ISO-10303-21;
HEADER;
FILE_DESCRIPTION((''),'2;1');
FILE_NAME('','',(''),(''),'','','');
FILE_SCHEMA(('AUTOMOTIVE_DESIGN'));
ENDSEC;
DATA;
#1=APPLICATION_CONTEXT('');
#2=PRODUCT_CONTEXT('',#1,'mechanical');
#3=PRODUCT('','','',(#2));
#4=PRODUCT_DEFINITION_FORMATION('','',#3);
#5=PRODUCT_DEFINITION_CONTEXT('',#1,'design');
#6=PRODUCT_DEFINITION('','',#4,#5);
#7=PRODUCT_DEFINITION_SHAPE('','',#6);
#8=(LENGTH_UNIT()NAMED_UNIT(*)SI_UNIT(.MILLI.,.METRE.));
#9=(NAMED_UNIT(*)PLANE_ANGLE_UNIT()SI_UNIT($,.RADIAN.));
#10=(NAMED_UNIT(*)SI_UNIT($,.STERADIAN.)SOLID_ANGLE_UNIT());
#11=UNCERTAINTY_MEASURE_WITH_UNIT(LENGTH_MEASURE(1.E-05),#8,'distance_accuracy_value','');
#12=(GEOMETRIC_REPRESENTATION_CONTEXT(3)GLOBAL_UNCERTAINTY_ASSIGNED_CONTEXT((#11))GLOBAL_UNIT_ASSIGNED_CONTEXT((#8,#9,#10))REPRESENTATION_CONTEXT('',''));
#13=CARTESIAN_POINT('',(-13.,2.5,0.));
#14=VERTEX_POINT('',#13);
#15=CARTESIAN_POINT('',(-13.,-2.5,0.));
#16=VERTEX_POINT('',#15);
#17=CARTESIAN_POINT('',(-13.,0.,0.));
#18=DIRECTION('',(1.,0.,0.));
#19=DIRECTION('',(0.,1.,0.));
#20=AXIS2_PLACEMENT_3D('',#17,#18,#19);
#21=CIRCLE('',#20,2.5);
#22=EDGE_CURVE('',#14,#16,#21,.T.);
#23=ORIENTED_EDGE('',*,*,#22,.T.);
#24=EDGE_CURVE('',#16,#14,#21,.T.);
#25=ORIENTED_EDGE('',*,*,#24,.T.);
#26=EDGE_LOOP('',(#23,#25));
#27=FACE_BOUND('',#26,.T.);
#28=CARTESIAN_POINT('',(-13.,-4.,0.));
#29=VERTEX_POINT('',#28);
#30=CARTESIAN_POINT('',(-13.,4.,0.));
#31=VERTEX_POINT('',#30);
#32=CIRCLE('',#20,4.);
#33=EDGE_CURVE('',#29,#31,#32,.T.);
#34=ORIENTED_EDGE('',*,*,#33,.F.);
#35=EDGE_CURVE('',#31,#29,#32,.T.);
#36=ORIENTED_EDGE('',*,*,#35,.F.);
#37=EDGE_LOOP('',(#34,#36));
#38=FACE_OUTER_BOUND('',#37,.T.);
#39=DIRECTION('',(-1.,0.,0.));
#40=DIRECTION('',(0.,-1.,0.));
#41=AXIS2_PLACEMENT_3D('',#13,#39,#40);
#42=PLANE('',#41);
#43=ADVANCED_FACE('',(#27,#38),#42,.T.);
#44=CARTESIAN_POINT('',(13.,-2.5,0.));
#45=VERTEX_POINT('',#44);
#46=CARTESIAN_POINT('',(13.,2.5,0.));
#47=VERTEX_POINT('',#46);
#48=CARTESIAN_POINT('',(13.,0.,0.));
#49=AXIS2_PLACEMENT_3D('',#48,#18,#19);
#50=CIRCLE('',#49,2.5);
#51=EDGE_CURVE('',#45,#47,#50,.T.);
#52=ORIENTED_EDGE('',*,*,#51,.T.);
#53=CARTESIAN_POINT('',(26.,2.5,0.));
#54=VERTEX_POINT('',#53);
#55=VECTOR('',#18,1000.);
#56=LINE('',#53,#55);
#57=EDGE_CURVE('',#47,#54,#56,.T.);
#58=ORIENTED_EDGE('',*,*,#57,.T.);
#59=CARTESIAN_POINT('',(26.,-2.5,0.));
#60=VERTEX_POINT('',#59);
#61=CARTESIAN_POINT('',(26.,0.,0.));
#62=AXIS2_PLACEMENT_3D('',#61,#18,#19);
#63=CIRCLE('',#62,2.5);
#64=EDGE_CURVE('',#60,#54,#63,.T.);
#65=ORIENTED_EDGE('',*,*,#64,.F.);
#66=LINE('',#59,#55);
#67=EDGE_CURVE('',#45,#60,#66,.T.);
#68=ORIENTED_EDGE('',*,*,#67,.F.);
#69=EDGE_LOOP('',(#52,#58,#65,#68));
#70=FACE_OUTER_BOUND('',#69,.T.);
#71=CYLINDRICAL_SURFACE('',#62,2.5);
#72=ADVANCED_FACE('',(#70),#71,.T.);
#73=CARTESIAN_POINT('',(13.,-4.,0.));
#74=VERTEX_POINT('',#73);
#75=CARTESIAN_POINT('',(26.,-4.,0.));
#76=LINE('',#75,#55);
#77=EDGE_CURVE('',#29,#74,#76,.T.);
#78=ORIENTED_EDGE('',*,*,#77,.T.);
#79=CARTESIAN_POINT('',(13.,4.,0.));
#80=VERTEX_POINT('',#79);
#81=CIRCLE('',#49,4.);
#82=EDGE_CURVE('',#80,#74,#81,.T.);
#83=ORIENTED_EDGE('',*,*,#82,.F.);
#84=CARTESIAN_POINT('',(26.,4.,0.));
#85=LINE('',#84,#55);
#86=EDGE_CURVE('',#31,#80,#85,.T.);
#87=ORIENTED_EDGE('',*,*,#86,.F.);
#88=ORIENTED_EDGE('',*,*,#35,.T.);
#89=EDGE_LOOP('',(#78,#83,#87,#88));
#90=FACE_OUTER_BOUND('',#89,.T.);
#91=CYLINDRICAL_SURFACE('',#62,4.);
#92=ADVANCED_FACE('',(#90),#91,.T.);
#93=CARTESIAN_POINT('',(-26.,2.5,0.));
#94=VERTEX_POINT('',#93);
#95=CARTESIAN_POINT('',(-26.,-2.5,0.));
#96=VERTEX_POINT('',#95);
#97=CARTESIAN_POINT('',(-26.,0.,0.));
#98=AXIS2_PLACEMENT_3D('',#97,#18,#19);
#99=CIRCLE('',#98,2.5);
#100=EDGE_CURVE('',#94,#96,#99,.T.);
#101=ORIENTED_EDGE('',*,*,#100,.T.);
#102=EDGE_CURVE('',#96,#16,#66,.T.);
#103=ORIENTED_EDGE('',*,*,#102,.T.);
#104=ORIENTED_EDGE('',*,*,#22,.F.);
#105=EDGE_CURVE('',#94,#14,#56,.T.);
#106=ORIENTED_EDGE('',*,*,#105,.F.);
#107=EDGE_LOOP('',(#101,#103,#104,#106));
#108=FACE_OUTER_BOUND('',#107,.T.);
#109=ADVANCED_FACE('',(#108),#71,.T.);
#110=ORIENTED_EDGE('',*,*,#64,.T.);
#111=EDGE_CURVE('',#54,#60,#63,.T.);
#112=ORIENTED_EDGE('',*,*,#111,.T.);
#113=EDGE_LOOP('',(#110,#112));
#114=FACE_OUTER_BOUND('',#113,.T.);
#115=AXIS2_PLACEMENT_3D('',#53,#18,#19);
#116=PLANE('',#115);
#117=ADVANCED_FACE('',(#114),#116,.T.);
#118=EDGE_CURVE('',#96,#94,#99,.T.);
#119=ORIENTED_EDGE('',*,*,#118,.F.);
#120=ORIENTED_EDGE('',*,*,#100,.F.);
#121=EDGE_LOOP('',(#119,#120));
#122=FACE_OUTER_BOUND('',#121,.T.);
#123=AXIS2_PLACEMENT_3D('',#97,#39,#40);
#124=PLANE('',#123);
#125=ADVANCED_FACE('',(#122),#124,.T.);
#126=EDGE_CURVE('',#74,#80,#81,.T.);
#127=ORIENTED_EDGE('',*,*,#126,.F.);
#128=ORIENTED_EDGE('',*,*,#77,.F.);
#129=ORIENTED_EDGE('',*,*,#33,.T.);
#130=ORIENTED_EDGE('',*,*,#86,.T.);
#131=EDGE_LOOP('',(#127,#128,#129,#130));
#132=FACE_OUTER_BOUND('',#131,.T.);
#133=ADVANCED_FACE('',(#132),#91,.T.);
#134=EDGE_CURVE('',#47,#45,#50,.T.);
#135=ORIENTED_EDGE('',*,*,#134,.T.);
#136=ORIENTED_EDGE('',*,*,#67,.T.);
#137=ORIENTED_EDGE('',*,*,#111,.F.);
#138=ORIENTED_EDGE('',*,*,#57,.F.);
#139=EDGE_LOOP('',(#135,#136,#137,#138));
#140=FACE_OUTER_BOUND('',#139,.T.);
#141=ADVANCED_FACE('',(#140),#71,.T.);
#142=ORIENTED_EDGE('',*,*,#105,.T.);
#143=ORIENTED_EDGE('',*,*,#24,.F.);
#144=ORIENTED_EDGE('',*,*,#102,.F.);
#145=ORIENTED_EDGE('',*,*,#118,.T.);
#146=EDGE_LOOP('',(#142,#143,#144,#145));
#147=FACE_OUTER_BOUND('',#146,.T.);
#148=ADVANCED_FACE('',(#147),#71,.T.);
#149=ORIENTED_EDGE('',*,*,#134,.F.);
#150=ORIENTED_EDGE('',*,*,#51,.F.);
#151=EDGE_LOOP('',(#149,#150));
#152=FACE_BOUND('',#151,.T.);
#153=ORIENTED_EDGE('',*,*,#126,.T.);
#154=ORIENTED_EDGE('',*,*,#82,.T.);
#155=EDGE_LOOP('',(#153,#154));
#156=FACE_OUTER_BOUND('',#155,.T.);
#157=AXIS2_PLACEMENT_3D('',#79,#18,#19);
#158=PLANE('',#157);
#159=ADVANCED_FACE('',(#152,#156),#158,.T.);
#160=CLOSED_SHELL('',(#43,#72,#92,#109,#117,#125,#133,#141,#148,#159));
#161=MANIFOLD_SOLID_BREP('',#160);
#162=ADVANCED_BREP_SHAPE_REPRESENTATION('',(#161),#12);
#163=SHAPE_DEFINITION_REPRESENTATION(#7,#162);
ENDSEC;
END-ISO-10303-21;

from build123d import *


with BuildPart() as part:
    # Sketch1 → Revolve1 (revolve)
    with BuildSketch(Plane.XY):
        Polygon((26, 0), (-26, 0), (-26, 2.5), (-13, 2.5), (-13, 4), (13, 4), (13, 2.5), (26, 2.5), align=None)
    revolve(axis=Axis((26, 0, 0), (-1, 0, 0)))


solid = part.part
